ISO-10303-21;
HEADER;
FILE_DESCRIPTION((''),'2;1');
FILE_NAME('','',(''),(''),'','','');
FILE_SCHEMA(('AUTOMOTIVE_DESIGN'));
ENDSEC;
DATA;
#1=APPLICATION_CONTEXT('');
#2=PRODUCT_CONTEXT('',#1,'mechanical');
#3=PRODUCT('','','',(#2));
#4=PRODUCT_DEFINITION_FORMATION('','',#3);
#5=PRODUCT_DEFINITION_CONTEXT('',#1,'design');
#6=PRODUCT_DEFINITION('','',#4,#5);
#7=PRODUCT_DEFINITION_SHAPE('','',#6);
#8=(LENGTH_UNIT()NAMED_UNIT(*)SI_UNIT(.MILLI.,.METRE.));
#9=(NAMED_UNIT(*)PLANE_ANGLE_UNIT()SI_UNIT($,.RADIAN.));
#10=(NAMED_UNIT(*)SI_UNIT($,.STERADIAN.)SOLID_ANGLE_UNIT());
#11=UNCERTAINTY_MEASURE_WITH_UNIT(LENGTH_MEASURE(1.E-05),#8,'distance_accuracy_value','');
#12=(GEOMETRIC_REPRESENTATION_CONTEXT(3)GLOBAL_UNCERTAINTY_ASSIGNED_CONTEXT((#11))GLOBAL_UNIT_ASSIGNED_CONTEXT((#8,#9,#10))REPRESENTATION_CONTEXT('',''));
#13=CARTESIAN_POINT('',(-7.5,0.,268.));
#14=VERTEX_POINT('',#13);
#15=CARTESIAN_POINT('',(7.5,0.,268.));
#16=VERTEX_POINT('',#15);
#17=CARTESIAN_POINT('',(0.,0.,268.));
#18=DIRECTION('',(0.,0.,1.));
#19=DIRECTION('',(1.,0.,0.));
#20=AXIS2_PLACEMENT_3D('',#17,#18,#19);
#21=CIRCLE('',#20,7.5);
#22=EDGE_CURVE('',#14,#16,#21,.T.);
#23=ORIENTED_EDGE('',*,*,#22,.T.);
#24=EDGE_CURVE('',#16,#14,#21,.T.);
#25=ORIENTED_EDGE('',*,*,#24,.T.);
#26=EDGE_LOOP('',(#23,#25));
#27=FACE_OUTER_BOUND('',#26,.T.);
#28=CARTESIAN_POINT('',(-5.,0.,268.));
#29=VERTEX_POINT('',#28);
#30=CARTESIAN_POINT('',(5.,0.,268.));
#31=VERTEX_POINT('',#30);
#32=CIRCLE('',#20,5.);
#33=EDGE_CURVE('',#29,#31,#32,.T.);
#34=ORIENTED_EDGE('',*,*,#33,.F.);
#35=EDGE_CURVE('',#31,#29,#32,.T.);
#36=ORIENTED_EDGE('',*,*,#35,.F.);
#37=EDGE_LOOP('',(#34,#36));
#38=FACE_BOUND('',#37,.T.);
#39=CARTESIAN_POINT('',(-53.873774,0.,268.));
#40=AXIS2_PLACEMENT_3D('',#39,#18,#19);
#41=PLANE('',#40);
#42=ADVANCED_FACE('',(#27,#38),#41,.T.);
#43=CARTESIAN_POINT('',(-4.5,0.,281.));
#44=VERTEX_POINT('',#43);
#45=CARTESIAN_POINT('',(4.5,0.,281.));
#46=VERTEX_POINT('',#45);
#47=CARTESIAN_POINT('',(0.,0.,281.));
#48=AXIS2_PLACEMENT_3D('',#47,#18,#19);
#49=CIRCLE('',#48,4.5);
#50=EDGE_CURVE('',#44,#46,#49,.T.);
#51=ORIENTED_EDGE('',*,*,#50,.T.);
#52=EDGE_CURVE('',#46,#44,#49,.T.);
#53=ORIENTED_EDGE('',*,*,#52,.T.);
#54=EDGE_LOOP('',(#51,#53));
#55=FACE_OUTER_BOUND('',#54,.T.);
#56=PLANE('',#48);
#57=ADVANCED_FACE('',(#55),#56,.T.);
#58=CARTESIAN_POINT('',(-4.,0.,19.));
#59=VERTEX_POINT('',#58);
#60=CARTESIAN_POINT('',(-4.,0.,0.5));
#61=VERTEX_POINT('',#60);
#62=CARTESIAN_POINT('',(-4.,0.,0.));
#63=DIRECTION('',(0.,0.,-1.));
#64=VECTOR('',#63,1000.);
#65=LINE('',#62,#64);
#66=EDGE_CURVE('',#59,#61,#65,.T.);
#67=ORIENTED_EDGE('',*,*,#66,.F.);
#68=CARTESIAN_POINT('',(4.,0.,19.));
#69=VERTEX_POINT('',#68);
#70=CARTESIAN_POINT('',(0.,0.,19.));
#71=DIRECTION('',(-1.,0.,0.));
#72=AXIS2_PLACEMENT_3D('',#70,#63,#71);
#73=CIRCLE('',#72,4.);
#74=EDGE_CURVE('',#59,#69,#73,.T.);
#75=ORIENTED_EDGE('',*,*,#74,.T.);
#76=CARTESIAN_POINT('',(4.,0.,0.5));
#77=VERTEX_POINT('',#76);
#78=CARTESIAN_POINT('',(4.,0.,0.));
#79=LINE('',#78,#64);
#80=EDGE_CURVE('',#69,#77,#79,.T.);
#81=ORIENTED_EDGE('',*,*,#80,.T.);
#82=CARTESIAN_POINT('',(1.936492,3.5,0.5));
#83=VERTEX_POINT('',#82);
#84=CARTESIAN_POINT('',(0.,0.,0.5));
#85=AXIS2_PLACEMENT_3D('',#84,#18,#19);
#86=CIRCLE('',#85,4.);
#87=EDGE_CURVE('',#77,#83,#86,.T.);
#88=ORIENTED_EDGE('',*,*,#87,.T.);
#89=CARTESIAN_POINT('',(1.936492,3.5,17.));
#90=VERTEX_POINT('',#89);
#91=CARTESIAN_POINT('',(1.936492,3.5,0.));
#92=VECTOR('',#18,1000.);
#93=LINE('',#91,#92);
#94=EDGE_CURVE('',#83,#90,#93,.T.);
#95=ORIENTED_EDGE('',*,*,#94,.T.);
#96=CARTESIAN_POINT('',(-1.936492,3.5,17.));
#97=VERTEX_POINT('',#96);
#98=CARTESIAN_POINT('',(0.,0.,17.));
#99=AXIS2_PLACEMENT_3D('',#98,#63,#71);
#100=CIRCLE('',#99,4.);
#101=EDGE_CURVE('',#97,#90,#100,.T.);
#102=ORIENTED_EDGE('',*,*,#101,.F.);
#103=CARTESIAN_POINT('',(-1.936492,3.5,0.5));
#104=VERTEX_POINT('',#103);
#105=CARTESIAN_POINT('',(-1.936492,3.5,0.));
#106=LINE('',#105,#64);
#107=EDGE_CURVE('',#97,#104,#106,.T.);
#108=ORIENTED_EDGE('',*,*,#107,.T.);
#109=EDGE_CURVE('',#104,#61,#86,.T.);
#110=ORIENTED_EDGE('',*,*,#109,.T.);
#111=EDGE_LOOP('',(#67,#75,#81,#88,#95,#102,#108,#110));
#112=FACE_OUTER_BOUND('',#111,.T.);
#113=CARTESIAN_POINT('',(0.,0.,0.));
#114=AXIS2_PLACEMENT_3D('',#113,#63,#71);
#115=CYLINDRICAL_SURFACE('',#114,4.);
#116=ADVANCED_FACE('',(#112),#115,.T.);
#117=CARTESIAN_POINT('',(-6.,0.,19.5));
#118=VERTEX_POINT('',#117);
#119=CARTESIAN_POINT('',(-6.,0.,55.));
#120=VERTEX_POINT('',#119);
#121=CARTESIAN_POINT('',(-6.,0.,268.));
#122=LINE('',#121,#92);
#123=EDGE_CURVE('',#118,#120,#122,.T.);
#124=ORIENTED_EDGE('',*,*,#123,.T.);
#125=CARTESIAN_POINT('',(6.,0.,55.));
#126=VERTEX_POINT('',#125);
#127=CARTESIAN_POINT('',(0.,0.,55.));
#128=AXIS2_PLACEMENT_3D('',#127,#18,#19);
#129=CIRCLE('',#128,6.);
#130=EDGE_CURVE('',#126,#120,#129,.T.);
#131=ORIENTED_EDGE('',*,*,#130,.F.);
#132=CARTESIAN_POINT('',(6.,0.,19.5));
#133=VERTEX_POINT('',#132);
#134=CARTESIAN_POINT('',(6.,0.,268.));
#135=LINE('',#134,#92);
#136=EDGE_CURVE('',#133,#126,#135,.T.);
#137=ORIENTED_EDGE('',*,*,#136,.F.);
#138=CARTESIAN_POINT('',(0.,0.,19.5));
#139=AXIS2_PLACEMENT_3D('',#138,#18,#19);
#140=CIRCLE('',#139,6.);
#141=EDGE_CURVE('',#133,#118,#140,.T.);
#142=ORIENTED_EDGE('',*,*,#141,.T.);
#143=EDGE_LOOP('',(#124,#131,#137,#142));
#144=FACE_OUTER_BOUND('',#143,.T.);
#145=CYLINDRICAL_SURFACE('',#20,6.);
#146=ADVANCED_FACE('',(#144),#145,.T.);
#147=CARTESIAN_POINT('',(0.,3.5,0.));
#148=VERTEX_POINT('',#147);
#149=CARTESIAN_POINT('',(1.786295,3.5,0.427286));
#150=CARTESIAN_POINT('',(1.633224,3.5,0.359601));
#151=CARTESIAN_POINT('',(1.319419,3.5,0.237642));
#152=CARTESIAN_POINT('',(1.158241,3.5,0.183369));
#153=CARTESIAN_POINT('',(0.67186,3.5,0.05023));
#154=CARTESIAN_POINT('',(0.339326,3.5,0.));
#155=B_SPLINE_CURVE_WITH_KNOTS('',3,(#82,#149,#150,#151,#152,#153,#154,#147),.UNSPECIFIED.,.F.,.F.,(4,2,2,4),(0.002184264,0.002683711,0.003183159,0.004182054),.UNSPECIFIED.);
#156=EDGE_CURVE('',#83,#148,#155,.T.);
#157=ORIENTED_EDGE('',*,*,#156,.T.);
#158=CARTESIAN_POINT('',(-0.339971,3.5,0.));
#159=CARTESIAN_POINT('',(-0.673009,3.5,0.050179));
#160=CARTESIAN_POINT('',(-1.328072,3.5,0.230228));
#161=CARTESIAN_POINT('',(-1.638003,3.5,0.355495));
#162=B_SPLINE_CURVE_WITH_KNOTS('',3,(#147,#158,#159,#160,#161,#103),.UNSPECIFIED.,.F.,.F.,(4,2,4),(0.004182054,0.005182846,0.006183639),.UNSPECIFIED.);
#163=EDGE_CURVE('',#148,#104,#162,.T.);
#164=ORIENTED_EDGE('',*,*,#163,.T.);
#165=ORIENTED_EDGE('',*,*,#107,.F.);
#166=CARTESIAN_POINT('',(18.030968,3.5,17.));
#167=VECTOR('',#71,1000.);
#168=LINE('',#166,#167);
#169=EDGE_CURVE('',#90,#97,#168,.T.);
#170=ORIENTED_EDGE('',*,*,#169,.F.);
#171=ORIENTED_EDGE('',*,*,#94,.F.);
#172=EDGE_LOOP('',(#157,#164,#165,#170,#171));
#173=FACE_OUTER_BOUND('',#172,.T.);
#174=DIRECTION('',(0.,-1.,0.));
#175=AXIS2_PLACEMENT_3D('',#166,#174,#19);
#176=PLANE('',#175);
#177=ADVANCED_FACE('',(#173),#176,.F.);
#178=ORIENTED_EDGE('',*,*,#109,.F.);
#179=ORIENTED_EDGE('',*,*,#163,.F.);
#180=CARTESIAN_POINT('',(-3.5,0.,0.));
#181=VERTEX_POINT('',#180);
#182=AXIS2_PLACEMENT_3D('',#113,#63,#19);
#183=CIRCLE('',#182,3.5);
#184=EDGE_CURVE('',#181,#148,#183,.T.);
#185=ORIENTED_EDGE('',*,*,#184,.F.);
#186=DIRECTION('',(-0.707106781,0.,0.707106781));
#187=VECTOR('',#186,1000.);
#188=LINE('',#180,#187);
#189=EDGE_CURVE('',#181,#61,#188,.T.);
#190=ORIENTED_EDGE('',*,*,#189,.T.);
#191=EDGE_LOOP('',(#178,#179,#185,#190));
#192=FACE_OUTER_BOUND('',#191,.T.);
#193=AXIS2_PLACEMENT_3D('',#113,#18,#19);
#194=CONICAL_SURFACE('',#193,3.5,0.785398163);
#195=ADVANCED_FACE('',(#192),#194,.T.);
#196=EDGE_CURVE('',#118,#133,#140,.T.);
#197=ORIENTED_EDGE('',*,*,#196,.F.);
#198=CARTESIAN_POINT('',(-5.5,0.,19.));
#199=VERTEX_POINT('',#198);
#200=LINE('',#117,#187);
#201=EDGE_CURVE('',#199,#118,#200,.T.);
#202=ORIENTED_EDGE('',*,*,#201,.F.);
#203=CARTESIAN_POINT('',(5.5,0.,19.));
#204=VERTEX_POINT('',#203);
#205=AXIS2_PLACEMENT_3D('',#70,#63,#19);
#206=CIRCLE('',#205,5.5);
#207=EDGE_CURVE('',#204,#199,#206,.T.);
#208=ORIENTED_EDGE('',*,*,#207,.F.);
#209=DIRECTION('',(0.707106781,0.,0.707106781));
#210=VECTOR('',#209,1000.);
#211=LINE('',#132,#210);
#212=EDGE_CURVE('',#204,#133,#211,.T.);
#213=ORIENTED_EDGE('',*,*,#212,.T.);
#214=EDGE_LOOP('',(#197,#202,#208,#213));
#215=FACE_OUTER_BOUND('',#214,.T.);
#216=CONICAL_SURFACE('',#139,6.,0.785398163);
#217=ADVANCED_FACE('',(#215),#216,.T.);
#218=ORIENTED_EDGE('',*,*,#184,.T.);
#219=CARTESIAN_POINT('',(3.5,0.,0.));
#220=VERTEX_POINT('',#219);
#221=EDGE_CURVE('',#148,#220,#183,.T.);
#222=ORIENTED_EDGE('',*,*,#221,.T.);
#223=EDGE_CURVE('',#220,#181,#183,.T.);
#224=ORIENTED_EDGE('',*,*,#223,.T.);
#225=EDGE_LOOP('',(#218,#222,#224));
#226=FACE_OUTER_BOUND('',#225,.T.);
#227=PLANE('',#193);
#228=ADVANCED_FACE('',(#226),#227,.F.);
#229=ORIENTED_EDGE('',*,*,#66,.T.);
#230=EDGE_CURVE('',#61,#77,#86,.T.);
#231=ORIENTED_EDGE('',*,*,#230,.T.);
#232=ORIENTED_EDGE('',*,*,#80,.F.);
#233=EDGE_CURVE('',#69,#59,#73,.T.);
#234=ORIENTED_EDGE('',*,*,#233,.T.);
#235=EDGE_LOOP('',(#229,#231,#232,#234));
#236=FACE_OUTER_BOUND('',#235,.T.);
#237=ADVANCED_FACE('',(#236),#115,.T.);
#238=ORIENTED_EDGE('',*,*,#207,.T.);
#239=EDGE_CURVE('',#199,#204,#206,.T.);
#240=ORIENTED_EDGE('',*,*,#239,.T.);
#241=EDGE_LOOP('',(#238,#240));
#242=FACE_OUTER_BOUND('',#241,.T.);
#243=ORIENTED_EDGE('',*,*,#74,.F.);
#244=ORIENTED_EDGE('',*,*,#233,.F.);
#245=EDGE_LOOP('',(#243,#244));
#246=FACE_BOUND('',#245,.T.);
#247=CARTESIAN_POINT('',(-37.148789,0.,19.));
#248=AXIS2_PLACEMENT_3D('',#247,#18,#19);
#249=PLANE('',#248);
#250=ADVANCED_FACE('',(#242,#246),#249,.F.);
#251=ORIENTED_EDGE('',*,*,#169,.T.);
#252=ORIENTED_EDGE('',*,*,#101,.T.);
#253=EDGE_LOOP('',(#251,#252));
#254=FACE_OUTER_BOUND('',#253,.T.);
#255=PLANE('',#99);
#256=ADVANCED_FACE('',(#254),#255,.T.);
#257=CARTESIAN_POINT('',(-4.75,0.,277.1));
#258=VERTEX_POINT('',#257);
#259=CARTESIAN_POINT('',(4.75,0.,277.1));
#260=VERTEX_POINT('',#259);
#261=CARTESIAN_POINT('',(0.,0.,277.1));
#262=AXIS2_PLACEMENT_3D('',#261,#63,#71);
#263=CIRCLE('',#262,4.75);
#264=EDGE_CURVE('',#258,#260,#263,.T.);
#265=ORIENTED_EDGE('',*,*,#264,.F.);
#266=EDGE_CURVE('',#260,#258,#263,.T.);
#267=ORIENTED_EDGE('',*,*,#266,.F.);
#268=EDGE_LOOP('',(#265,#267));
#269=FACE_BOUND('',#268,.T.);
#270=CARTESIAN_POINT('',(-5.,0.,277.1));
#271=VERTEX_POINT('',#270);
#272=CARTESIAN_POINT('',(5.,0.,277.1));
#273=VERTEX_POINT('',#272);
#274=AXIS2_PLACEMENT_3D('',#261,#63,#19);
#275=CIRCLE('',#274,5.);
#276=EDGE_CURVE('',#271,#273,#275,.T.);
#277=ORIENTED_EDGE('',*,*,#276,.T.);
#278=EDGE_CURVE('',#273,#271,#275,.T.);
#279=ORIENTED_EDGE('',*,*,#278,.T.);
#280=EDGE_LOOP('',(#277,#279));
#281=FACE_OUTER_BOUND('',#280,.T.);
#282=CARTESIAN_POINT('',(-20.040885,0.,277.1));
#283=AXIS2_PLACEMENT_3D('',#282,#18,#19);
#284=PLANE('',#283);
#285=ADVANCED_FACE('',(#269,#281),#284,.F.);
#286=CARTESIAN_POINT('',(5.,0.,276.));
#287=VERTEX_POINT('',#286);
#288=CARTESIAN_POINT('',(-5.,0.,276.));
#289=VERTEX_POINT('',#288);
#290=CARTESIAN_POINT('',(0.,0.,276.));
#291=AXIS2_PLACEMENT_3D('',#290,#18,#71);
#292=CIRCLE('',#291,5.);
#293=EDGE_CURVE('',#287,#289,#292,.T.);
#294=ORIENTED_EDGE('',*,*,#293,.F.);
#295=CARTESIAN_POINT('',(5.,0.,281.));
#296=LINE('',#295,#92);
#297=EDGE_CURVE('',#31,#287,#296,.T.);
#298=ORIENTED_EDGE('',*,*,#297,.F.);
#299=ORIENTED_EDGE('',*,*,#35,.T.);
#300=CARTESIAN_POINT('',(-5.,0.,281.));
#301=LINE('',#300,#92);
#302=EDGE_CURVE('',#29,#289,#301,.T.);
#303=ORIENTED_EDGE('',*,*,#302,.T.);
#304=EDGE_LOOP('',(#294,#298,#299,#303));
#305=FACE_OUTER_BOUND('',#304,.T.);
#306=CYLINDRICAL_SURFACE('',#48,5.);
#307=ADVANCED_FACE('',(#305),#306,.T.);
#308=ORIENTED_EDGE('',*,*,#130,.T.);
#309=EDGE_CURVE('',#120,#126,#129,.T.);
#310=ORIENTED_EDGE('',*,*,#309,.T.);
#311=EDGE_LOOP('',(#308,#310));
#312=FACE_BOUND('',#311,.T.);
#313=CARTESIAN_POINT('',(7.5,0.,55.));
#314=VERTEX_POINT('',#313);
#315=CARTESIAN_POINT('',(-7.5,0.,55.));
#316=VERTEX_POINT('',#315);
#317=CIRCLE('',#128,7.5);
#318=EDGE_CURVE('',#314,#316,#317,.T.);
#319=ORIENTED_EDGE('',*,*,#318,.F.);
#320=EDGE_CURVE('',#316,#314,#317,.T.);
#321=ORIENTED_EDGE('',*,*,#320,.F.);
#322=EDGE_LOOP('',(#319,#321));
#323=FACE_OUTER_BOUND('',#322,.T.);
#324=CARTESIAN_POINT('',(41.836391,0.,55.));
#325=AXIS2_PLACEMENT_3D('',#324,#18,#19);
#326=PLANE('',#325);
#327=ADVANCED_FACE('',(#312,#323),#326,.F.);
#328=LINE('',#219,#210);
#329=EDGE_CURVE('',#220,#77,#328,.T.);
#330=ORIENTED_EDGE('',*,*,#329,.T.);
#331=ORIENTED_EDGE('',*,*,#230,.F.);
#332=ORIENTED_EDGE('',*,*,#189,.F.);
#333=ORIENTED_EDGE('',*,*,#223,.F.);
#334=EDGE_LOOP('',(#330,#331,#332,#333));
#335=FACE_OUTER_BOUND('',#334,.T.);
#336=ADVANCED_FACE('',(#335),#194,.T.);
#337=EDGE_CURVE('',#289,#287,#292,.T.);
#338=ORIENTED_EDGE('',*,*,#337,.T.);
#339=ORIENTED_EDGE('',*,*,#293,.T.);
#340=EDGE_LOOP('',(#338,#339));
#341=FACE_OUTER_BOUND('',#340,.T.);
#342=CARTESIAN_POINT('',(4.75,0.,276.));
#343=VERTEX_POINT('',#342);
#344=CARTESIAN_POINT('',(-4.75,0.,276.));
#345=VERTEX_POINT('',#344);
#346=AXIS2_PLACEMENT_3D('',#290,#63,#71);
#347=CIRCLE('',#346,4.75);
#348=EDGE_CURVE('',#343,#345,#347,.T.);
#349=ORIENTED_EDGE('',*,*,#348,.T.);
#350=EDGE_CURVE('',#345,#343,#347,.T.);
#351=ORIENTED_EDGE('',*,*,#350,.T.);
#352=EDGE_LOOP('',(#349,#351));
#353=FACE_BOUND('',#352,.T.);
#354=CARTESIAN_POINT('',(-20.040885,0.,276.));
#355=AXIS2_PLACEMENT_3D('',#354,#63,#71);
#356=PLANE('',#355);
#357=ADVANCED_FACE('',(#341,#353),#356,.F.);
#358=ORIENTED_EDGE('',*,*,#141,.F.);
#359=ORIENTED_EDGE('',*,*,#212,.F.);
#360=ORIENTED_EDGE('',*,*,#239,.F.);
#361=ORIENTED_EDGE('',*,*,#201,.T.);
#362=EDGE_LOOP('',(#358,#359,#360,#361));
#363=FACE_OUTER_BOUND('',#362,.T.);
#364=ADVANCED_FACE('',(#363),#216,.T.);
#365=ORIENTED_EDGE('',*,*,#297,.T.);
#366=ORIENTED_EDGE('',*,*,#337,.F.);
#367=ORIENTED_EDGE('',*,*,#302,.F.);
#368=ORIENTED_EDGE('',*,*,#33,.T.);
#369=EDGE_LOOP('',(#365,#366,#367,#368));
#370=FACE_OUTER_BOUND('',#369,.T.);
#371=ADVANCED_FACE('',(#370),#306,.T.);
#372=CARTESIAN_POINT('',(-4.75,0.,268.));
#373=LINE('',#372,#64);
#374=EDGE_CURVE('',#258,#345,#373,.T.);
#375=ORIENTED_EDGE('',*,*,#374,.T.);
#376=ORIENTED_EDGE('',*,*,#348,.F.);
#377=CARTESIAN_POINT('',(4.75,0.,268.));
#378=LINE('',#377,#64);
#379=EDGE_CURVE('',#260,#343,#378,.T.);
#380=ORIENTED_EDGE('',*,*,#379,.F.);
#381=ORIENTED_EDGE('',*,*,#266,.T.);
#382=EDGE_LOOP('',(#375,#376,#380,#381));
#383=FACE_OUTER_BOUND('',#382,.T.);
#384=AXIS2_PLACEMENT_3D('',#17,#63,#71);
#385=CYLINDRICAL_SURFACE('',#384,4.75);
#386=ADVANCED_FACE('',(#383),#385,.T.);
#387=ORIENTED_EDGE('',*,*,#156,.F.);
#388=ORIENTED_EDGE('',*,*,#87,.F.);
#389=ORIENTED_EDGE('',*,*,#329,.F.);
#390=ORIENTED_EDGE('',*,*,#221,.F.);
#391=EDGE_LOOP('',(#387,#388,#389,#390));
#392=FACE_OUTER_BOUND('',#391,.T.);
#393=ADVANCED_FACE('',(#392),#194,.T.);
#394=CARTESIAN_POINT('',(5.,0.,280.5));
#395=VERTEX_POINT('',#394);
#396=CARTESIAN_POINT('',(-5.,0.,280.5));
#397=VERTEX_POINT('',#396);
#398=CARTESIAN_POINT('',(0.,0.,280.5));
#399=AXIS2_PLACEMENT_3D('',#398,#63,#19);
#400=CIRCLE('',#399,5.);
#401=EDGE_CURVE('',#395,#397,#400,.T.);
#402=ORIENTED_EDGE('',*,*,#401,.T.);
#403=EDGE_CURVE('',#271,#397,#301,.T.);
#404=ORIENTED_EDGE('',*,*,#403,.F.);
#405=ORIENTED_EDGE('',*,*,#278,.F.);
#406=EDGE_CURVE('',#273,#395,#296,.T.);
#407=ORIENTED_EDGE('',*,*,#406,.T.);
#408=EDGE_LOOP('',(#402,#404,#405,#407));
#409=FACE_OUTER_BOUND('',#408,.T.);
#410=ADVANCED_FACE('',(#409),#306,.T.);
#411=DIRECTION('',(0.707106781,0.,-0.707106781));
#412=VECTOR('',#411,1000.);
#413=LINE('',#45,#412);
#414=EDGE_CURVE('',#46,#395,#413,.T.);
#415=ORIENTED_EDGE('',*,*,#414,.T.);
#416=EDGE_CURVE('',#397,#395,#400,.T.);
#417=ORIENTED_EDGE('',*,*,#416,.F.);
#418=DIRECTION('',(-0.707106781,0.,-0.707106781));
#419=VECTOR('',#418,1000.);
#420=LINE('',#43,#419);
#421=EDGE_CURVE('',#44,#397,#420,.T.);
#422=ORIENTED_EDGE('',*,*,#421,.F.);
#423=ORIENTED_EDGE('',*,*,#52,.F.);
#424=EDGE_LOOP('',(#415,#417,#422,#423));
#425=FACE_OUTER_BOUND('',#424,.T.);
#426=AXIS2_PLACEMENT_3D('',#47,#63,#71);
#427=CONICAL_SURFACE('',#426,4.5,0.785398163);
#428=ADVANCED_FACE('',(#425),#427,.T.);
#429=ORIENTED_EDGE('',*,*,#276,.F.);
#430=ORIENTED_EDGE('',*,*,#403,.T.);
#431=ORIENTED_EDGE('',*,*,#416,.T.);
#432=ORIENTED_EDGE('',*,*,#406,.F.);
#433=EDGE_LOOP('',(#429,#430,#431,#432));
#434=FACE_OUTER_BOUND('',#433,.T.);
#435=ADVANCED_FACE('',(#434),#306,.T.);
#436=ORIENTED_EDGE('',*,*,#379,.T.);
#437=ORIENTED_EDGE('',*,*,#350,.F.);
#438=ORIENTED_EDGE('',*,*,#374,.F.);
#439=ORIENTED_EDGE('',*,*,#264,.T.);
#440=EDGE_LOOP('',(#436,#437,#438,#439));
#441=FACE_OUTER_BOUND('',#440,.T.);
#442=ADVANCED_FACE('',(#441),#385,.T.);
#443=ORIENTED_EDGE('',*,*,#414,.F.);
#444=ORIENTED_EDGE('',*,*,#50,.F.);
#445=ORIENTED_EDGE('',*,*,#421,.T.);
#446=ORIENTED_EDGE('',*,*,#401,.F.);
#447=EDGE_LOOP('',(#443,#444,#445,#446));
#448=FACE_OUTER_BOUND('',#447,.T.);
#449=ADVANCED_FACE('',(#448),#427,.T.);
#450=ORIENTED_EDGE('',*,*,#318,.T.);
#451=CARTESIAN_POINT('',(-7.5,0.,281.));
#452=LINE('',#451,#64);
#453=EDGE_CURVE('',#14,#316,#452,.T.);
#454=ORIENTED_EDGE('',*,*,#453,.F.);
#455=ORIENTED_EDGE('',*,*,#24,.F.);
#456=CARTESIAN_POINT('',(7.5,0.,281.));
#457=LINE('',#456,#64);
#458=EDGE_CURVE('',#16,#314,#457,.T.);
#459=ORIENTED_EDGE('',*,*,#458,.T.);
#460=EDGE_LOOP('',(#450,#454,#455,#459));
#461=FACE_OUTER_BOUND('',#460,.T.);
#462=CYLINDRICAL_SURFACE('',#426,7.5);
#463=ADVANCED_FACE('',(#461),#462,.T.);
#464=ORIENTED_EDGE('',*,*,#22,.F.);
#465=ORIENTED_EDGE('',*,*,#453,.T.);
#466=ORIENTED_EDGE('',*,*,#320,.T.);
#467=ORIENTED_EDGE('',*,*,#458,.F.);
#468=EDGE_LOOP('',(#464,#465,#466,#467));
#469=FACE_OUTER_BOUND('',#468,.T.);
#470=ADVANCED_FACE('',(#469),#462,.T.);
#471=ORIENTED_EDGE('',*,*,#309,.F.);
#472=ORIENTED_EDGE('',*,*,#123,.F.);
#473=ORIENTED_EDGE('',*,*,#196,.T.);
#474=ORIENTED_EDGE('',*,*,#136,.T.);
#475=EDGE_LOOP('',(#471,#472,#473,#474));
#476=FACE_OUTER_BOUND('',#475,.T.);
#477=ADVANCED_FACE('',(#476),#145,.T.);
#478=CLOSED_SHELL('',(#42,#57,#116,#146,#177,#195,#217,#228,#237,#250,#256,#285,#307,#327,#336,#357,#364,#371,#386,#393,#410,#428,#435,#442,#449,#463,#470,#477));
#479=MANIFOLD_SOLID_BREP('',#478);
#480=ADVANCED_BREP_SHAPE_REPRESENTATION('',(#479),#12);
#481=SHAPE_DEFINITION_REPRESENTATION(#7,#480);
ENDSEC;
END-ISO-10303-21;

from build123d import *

# Parameters (mm, degrees)
SKETCH_1_R          = 7.5
EXTRUDE_1_DEPTH     = 281
SKETCH_3_W          = 48.87377388
SKETCH_3_H          = 13
SKETCH_4_W          = 35.83639091
SKETCH_4_H          = 82.680612398
SKETCH_8_W          = 33.14878911
SKETCH_8_H          = 39.753572134
CHAMFER_2_SIZE      = 0.5
SKETCH_15_W         = 15.290885205
SKETCH_15_H         = 1.1
CHAMFER_3_SIZE      = 0.5
SKETCH_16_W         = 27.071895425
SKETCH_16_H         = 14.859010271
CUT_EXTRUDE_1_DEPTH = 17


with BuildPart() as part:
    # 草图1 → 凸台-拉伸1 (new body)
    with BuildSketch(Plane.XY):
        Circle(SKETCH_1_R)
    extrude(amount=EXTRUDE_1_DEPTH)

    # 草图3 → 切除-旋转1 (revolve, cut)
    with BuildSketch(Plane(origin=(0, 0, 0), x_dir=(1, 0, 0), z_dir=(0, 1, 0)), mode=Mode.PRIVATE) as cut_revolve_1_sk:
        with Locations((-29.43688694, -274.5)):
            Rectangle(SKETCH_3_W, SKETCH_3_H)
    revolve(cut_revolve_1_sk.sketch.rotate(Axis((0, 0, 281), (0, 0, -1)), 180), axis=Axis((0, 0, 281), (0, 0, -1)), mode=Mode.SUBTRACT)

    # 草图4 → 切除-旋转2 (revolve, cut)
    with BuildSketch(Plane(origin=(0, 0, 0), x_dir=(1, 0, 0), z_dir=(0, 1, 0))):
        with Locations((23.918195455, -13.659693801)):
            Rectangle(SKETCH_4_W, SKETCH_4_H)
    revolve(axis=Axis((0, 0, 281), (0, 0, -1)), mode=Mode.SUBTRACT)

    # 草图8 → 切除-旋转5 (revolve, cut)
    with BuildSketch(Plane(origin=(0, 0, 0), x_dir=(1, 0, 0), z_dir=(0, 1, 0)), mode=Mode.PRIVATE) as cut_revolve_5_sk:
        with Locations((-20.574394555, 0.876786067)):
            Rectangle(SKETCH_8_W, SKETCH_8_H)
    revolve(cut_revolve_5_sk.sketch.rotate(Axis((0, 0, 268), (0, 0, 1)), 180), axis=Axis((0, 0, 268), (0, 0, 1)), mode=Mode.SUBTRACT)

    # 倒角2
    chamfer_2_edges = [part.edges().sort_by_distance(p)[0] for p in [
        (-6, 0, 19),
        (-4, 0, 0),
    ]]
    chamfer(chamfer_2_edges, length=CHAMFER_2_SIZE)

    # 草图15 → 切除-旋转7 (revolve, cut)
    with BuildSketch(Plane(origin=(0, 0, 0), x_dir=(1, 0, 0), z_dir=(0, 1, 0)), mode=Mode.PRIVATE) as cut_revolve_7_sk:
        with Locations((-12.395442603, -276.55)):
            Rectangle(SKETCH_15_W, SKETCH_15_H)
    revolve(cut_revolve_7_sk.sketch.rotate(Axis((0, 0, 281), (0, 0, 1)), 180), axis=Axis((0, 0, 281), (0, 0, 1)), mode=Mode.SUBTRACT)

    # 倒角3
    chamfer_3_edges = [part.edges().sort_by_distance(p)[0] for p in [
        (-5, 0, 281),
    ]]
    chamfer(chamfer_3_edges, length=CHAMFER_3_SIZE)

    # 草图16 → 切除-拉伸1 (cut)
    with BuildSketch(Plane(origin=(0, 0, 0), x_dir=(-1, 0, 0), z_dir=(0, 0, -1))):
        with Locations((-4.49502023, 10.929505136)):
            Rectangle(SKETCH_16_W, SKETCH_16_H)
    extrude(amount=-CUT_EXTRUDE_1_DEPTH, mode=Mode.SUBTRACT)


solid = part.part
